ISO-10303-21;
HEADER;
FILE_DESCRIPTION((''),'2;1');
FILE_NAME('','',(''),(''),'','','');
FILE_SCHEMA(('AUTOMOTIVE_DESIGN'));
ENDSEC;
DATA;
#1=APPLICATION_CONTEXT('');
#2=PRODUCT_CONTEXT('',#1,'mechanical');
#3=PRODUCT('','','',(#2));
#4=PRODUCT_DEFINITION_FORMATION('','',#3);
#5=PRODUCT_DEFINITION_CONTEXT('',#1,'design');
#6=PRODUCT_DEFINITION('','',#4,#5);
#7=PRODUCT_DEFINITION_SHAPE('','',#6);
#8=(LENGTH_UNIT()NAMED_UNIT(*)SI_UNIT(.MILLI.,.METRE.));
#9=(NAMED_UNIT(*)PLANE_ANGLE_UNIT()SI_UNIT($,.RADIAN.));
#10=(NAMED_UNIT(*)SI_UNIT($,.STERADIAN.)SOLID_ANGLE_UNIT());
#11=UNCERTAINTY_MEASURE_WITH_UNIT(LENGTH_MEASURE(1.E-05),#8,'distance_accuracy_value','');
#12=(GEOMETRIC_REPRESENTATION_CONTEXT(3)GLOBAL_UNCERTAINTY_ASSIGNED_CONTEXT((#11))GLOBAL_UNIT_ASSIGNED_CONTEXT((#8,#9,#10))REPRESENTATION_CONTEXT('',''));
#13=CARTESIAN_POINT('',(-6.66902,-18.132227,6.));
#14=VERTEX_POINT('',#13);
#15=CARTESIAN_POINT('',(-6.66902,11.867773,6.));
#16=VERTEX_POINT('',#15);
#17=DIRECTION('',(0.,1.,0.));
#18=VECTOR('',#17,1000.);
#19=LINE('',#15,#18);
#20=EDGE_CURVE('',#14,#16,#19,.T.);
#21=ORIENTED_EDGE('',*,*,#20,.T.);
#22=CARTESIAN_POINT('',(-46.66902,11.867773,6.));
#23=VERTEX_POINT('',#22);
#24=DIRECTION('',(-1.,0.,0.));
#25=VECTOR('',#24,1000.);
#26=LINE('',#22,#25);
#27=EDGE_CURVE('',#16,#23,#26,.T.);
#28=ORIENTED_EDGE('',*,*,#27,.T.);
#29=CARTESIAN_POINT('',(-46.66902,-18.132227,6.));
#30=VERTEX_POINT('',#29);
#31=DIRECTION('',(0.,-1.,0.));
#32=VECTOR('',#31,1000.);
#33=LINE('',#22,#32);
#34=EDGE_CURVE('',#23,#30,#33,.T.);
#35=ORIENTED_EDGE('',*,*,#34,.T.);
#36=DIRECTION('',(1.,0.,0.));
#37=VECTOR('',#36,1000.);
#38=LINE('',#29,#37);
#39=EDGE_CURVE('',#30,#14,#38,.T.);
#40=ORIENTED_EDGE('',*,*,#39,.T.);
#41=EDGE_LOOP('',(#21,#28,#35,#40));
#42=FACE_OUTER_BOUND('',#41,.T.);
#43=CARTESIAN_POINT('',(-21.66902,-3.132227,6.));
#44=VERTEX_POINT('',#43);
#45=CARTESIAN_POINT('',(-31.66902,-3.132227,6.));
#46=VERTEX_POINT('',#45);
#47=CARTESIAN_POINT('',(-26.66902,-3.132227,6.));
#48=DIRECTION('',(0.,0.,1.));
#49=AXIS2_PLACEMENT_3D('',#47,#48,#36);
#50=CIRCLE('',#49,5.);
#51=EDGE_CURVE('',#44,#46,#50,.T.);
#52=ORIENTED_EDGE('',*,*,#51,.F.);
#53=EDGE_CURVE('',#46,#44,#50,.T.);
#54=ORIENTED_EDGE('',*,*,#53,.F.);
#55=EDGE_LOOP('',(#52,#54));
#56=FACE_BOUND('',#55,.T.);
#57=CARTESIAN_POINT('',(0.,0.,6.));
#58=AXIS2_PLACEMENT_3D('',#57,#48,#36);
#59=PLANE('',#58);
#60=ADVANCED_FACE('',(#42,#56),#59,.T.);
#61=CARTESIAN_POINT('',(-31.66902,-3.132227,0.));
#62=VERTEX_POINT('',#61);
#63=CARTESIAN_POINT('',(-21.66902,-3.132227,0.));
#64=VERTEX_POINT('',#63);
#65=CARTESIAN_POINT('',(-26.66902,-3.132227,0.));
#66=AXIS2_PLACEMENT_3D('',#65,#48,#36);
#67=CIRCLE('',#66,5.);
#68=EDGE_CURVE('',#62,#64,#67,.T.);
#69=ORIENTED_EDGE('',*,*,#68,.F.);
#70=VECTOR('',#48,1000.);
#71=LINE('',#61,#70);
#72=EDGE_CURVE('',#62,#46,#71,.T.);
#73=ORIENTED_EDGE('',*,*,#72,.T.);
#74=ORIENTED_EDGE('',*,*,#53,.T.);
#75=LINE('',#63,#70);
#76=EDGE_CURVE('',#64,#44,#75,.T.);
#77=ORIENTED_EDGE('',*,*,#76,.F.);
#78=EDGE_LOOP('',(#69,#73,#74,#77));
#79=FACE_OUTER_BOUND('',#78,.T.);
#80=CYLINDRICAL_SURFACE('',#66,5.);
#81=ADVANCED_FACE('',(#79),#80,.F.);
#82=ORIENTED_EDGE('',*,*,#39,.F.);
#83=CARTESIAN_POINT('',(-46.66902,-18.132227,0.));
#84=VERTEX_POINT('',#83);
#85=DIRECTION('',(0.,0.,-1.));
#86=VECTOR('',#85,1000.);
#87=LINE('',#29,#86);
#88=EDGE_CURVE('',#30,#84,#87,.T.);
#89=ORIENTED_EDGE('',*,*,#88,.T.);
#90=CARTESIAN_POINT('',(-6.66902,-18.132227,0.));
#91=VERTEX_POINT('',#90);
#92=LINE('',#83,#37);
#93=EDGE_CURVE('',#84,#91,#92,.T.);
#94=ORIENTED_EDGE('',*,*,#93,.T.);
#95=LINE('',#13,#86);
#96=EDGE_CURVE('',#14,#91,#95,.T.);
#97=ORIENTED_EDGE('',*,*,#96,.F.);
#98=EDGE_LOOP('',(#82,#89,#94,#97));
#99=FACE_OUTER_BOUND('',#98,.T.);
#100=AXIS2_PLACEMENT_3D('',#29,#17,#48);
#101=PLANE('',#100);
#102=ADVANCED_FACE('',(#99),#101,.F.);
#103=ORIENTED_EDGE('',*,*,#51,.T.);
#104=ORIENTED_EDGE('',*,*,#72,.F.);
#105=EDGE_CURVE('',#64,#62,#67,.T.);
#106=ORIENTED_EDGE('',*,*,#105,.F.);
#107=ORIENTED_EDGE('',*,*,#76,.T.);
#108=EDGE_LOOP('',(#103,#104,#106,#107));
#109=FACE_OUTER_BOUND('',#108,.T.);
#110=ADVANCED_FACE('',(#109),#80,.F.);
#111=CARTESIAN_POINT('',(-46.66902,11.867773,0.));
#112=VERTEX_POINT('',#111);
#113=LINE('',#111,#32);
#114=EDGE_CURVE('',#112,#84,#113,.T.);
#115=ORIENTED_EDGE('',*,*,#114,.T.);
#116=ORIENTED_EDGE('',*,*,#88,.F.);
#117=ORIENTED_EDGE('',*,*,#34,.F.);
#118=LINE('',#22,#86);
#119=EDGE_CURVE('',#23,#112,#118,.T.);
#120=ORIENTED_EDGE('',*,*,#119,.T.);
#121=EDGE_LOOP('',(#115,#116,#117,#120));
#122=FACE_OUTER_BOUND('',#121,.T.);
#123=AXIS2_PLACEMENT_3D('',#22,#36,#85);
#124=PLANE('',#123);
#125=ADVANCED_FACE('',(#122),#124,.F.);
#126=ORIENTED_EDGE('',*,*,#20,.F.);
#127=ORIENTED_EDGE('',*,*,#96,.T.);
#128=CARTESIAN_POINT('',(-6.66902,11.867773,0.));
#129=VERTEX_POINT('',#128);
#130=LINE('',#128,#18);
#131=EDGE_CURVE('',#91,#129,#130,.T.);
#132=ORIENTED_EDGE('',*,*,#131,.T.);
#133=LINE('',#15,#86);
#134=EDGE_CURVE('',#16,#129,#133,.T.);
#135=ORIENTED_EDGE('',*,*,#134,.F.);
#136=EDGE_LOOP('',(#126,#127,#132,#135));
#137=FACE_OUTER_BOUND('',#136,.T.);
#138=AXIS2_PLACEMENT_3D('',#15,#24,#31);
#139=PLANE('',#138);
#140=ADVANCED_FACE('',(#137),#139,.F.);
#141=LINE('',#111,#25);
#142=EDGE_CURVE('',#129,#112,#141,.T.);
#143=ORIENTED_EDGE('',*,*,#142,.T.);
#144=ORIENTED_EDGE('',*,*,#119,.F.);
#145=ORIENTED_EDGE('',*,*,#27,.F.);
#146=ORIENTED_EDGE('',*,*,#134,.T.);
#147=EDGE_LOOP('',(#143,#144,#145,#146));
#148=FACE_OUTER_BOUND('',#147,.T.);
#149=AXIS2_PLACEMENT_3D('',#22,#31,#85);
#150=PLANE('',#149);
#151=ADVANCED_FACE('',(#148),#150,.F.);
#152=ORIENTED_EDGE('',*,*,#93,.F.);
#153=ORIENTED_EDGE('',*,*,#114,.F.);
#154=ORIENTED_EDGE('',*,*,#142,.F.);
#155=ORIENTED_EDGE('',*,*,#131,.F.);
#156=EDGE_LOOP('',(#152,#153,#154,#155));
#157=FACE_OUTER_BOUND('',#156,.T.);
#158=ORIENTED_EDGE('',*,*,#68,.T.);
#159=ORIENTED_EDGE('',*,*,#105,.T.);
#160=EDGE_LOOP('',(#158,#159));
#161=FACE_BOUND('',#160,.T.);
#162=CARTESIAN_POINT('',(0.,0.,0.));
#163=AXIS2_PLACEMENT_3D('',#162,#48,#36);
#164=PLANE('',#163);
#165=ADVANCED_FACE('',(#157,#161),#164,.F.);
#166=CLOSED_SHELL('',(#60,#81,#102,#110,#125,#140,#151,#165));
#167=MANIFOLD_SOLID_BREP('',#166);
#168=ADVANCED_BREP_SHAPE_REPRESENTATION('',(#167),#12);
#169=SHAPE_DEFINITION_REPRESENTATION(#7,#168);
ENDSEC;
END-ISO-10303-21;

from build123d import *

# Parameters (mm, degrees)
SKETCH1_W           = 40
SKETCH1_H           = 30
BOSS_EXTRUDE1_DEPTH = 6
SKETCH2_R           = 5
CUT_EXTRUDE1_DEPTH  = 6


with BuildPart() as part:
    # Sketch1 → Boss-Extrude1 (new body)
    with BuildSketch(Plane.XY):
        with Locations((-26.669019685, -3.132226563)):
            Rectangle(SKETCH1_W, SKETCH1_H)
    extrude(amount=BOSS_EXTRUDE1_DEPTH)

    # Sketch2 → Cut-Extrude1 (cut)
    with BuildSketch(Plane.XY.offset(6)):
        with Locations((-26.669019685, -3.132226563)):
            Circle(SKETCH2_R)
    extrude(amount=-CUT_EXTRUDE1_DEPTH, mode=Mode.SUBTRACT)


solid = part.part
